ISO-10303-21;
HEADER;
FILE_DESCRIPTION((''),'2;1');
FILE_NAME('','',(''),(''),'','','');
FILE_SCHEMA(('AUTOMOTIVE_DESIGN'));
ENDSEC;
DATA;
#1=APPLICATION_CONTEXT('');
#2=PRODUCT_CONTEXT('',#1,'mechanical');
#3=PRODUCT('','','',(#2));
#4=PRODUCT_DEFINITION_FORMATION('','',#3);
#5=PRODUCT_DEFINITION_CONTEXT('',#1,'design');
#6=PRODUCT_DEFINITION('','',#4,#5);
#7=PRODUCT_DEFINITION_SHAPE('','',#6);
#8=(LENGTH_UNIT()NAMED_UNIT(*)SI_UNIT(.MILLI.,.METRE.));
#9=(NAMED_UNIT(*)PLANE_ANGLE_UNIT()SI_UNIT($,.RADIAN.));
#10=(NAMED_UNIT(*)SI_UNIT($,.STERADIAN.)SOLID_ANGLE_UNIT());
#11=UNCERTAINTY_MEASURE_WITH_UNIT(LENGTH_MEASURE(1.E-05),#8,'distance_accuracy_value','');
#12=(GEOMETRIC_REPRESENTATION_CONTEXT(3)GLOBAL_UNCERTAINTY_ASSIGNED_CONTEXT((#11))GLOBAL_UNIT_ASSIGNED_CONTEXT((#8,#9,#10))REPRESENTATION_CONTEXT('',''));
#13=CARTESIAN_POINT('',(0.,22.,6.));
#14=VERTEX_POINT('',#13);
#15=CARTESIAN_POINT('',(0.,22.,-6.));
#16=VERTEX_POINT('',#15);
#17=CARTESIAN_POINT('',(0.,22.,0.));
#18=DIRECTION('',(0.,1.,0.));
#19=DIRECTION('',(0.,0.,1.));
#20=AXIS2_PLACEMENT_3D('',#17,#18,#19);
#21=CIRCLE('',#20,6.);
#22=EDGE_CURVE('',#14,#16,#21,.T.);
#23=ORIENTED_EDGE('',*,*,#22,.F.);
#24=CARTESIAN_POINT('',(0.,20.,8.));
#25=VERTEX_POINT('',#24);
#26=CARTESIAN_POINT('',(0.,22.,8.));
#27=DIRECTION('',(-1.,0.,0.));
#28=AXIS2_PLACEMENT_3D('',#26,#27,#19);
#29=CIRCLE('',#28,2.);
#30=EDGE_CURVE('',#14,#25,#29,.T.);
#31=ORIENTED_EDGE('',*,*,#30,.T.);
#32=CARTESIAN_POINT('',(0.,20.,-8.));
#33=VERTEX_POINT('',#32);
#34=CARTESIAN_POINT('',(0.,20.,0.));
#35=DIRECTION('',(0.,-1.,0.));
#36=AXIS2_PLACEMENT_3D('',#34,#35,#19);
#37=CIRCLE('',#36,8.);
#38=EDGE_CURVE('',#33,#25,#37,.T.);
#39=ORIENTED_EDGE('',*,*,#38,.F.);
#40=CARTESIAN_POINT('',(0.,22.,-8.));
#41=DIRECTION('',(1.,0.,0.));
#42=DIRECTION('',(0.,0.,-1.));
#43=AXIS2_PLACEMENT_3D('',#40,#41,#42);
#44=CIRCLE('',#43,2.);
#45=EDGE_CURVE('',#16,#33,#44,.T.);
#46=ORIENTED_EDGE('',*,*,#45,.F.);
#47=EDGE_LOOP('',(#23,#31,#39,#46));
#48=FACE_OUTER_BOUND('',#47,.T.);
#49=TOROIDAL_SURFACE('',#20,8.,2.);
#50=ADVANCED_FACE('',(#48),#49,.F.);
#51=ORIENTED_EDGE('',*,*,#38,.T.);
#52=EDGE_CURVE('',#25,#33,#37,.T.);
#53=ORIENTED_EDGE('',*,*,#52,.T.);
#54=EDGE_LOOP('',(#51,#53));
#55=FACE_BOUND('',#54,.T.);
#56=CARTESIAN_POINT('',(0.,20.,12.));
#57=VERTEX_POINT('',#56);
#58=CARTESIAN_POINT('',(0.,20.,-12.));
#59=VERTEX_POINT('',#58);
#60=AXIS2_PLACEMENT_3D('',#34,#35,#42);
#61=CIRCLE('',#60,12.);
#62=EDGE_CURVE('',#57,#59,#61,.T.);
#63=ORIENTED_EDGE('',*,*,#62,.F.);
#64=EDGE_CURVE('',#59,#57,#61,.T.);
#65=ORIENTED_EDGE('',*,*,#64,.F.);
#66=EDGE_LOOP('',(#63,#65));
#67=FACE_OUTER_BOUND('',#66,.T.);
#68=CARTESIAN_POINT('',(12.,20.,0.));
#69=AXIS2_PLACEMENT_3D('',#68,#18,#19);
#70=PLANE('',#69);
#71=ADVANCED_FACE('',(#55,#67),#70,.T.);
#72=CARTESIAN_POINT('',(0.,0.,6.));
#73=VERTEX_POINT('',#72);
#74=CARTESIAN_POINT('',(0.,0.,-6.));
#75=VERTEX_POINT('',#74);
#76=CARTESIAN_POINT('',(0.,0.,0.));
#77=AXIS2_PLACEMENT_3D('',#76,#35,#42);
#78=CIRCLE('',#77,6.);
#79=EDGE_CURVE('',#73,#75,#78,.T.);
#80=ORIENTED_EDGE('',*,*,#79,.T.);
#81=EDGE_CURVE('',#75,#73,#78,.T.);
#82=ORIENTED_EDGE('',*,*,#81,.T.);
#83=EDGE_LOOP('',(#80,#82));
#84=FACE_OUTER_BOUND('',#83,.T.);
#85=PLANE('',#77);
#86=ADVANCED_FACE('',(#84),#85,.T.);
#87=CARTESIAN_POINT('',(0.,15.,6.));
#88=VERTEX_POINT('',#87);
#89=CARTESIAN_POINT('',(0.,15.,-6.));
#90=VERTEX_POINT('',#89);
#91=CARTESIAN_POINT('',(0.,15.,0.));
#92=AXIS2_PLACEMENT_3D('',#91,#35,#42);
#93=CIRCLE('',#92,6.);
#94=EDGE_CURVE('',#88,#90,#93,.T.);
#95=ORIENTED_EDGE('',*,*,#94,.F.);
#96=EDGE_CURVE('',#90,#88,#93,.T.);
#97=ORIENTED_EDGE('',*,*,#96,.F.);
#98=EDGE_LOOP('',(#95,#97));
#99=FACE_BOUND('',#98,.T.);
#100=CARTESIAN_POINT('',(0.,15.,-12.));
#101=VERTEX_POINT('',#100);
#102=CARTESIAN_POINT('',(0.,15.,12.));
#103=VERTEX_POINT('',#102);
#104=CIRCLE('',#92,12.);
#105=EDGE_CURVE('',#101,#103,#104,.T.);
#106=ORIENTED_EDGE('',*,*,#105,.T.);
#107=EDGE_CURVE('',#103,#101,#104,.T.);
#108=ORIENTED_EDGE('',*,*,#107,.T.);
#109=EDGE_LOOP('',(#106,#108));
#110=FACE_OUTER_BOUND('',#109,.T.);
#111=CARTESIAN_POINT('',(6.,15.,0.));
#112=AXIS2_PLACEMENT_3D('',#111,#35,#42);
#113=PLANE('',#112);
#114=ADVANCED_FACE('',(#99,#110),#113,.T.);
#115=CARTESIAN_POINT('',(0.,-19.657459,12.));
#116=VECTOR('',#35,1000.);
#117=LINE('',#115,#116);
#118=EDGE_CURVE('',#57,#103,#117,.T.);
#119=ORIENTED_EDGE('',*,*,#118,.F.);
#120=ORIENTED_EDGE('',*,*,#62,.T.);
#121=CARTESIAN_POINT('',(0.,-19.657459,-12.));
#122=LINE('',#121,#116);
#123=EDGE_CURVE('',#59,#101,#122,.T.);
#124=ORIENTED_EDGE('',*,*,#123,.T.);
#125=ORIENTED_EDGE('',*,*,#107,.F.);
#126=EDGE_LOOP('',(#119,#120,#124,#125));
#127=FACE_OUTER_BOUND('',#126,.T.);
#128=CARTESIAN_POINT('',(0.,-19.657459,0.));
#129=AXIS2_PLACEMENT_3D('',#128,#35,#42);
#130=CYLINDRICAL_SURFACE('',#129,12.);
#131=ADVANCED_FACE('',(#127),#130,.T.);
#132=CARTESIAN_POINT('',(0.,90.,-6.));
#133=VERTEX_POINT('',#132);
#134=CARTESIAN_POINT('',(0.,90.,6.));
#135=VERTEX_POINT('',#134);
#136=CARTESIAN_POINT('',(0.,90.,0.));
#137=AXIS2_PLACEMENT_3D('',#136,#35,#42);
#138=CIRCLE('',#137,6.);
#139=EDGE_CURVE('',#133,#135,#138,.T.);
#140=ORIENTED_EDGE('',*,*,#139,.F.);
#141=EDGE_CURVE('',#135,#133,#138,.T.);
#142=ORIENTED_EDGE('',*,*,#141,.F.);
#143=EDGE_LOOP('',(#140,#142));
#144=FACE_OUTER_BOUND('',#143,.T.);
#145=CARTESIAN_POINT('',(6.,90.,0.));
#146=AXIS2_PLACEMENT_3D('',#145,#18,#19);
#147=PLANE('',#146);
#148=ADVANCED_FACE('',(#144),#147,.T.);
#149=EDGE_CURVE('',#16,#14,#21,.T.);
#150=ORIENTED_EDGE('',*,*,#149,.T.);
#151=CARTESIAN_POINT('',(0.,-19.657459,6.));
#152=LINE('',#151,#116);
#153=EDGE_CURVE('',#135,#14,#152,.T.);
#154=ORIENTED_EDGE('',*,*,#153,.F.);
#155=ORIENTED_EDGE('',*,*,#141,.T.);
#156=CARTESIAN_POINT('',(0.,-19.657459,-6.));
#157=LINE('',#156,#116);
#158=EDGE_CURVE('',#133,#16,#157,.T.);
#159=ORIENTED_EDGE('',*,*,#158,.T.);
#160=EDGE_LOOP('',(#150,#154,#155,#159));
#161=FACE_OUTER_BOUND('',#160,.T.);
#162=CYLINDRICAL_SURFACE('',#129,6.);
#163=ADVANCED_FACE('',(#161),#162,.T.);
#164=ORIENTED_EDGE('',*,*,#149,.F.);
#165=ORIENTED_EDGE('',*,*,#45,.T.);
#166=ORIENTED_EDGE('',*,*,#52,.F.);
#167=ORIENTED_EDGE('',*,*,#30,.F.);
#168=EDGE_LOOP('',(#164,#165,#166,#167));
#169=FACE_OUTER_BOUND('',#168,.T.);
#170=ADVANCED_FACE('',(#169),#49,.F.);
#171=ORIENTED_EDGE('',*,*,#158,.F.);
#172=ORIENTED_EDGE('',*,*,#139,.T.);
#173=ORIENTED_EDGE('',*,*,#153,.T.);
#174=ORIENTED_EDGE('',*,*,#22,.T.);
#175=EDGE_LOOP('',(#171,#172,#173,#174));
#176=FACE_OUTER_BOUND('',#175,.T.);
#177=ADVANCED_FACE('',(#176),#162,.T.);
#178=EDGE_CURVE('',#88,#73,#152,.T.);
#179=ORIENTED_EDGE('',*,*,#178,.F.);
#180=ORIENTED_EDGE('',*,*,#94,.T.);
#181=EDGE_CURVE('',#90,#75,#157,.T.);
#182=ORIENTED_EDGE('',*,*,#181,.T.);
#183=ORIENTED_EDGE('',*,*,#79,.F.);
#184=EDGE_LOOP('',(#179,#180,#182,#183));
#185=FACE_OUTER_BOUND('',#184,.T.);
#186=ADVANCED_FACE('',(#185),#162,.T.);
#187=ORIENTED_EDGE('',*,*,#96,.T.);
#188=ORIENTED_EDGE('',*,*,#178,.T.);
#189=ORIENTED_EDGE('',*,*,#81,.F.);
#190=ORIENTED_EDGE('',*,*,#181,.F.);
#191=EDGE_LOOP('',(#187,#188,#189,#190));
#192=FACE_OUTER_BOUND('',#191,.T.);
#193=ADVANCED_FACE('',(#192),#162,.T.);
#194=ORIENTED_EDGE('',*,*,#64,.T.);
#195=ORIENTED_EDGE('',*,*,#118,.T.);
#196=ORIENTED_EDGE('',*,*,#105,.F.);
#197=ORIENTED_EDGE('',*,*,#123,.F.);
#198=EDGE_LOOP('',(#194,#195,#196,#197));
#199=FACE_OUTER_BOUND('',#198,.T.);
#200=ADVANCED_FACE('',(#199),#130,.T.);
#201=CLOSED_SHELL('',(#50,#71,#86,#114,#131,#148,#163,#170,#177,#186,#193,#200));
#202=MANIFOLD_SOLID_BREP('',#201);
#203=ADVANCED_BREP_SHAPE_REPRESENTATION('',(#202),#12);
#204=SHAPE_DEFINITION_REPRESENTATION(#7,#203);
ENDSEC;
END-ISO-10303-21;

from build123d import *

# Parameters (mm, degrees)
COLLAR_FILLET_R2_R = 2


with BuildPart() as part:
    # Stud Profile Sketch → Stud Body Revolve (revolve)
    with BuildSketch(Plane.XY, mode=Mode.PRIVATE) as stud_body_revolve_sk:
        Polygon((0, 0), (6, 0), (6, 15), (12, 15), (12, 20), (6, 20), (6, 90), (0, 90), align=None)
    revolve(stud_body_revolve_sk.sketch.rotate(Axis((0, -19.657458564, 0), (0, 1, 0)), 90), axis=Axis((0, -19.657458564, 0), (0, 1, 0)))

    # Collar Fillet R2
    collar_fillet_r2_edges = [part.edges().sort_by_distance(p)[0] for p in [
        (0, 20, 6),
    ]]
    fillet(collar_fillet_r2_edges, radius=COLLAR_FILLET_R2_R)


solid = part.part
